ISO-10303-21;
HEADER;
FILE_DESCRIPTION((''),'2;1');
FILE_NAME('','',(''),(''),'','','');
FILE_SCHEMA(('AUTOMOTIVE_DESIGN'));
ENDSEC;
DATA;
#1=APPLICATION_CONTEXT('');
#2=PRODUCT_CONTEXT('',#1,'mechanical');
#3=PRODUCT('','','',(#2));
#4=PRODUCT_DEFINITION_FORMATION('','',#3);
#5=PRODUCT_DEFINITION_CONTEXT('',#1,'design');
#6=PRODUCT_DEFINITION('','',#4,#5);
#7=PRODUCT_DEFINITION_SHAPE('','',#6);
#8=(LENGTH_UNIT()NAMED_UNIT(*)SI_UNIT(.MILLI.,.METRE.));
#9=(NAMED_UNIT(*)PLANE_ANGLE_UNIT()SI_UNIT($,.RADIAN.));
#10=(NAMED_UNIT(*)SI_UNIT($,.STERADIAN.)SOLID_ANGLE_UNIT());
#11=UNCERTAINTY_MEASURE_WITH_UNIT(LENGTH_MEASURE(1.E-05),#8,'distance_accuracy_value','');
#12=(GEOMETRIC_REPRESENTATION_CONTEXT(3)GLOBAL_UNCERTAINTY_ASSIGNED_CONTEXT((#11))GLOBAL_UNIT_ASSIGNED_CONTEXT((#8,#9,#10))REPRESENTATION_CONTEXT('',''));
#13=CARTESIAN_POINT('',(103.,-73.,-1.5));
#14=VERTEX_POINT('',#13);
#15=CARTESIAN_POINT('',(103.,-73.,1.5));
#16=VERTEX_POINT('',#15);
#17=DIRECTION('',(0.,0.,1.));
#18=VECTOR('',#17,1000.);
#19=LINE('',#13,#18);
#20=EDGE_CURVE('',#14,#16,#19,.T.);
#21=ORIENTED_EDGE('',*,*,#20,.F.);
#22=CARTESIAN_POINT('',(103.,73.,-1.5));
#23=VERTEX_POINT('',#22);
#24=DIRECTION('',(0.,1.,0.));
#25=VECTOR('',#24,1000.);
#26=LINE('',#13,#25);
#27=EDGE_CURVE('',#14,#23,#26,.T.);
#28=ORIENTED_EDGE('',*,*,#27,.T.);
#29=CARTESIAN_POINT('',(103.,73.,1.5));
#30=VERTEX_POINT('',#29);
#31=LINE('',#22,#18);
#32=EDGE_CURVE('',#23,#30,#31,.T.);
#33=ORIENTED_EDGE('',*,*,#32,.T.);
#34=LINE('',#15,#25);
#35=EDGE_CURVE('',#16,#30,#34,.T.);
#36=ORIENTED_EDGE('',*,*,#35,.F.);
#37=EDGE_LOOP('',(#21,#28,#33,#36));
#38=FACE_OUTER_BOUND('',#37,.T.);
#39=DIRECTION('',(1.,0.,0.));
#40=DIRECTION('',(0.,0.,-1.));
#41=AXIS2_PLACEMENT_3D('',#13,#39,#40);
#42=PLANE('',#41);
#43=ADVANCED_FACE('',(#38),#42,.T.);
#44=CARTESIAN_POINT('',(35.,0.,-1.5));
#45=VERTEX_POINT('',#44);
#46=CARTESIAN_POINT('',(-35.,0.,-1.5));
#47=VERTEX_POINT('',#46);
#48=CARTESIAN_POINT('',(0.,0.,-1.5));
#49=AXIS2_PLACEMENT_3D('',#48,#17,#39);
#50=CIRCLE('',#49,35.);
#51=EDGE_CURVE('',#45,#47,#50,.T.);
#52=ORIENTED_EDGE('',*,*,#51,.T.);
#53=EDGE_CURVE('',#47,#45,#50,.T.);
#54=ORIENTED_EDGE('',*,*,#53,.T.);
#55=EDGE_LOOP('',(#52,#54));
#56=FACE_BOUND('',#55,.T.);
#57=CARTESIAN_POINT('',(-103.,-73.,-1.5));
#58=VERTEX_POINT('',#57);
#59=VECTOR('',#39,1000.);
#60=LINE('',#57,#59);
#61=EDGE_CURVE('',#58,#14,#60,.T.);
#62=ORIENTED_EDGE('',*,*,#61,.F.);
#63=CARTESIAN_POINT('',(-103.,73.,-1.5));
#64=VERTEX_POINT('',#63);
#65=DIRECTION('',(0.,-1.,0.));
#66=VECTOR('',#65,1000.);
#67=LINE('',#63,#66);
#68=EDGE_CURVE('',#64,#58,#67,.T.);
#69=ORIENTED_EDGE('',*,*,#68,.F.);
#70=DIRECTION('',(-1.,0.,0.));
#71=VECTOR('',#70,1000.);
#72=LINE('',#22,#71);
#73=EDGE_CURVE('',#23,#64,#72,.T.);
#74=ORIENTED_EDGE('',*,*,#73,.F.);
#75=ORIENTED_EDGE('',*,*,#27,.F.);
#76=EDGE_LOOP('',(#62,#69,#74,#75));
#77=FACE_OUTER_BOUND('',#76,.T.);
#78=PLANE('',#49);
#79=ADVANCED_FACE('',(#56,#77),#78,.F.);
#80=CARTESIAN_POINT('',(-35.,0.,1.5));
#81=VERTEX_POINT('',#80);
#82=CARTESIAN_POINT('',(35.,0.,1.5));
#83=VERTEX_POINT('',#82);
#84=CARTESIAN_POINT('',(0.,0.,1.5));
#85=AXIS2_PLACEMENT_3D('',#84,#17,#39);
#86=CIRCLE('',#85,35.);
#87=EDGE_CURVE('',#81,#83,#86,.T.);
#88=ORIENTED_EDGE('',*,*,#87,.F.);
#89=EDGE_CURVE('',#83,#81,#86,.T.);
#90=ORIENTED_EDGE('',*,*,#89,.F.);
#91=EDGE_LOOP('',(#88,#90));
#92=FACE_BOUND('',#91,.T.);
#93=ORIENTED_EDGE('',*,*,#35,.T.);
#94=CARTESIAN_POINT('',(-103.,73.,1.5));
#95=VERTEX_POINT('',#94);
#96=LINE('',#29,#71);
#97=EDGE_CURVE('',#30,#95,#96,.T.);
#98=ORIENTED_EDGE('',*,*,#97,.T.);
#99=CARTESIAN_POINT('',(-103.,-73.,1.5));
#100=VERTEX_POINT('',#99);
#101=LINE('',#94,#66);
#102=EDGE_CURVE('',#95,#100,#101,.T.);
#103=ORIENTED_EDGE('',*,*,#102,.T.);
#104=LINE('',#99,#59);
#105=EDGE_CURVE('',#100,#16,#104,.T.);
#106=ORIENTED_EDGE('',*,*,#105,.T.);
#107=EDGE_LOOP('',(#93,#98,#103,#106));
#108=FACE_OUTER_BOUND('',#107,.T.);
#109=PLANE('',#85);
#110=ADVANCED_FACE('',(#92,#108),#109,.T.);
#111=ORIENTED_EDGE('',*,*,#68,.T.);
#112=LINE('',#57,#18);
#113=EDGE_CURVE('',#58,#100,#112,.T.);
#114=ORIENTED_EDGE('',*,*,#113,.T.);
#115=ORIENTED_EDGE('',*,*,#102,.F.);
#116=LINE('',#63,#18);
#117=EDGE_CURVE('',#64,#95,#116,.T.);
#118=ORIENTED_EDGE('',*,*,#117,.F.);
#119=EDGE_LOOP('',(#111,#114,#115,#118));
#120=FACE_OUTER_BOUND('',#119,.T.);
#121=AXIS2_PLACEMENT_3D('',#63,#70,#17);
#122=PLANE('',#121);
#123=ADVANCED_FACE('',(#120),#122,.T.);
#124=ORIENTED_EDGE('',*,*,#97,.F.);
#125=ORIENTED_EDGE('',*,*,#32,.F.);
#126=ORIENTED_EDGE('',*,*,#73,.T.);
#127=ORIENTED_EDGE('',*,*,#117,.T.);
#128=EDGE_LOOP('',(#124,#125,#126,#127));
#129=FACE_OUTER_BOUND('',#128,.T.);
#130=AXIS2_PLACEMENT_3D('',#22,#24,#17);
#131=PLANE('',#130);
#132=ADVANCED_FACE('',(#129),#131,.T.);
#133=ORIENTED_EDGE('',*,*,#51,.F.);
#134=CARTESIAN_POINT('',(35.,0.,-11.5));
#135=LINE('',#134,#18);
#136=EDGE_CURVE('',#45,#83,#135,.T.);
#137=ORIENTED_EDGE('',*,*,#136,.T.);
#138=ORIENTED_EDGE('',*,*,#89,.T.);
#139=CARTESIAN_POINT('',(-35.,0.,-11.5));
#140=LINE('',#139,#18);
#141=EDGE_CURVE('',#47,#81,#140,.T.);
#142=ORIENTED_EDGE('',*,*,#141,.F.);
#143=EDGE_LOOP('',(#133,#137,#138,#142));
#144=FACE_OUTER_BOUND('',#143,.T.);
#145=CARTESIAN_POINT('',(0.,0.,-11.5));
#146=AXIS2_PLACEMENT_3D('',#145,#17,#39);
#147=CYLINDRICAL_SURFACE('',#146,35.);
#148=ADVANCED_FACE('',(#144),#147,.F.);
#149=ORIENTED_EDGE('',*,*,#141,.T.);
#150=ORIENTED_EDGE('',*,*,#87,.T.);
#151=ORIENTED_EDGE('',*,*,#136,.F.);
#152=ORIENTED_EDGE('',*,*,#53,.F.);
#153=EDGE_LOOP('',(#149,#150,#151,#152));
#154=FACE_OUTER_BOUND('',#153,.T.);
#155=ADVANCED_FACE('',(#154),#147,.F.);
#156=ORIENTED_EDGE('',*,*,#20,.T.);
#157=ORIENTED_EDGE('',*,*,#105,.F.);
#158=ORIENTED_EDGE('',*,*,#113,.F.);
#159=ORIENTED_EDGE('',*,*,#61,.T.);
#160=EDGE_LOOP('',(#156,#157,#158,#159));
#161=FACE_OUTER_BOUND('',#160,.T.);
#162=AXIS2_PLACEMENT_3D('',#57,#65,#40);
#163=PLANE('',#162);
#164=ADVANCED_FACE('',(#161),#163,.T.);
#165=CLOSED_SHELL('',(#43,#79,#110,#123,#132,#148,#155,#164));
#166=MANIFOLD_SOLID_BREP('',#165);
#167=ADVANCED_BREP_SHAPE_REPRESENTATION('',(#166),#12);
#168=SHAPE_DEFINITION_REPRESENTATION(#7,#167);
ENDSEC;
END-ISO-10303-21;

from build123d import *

# Parameters (mm, degrees)
SKETCH_1_W          = 206
SKETCH_1_H          = 146
EXTRUDE_1_DEPTH     = 1.5
SKETCH_2_R          = 35
CUT_EXTRUDE_1_DEPTH = 11.5


with BuildPart() as part:
    # 草图1 → 凸台-拉伸1 (new, symmetric)
    with BuildSketch(Plane.XY):
        Rectangle(SKETCH_1_W, SKETCH_1_H)
    extrude(amount=EXTRUDE_1_DEPTH, both=True)

    # 草图2 → 切除-拉伸1 (cut, symmetric)
    with BuildSketch(Plane.XY):
        Circle(SKETCH_2_R)
    extrude(amount=CUT_EXTRUDE_1_DEPTH, both=True, mode=Mode.SUBTRACT)


solid = part.part
